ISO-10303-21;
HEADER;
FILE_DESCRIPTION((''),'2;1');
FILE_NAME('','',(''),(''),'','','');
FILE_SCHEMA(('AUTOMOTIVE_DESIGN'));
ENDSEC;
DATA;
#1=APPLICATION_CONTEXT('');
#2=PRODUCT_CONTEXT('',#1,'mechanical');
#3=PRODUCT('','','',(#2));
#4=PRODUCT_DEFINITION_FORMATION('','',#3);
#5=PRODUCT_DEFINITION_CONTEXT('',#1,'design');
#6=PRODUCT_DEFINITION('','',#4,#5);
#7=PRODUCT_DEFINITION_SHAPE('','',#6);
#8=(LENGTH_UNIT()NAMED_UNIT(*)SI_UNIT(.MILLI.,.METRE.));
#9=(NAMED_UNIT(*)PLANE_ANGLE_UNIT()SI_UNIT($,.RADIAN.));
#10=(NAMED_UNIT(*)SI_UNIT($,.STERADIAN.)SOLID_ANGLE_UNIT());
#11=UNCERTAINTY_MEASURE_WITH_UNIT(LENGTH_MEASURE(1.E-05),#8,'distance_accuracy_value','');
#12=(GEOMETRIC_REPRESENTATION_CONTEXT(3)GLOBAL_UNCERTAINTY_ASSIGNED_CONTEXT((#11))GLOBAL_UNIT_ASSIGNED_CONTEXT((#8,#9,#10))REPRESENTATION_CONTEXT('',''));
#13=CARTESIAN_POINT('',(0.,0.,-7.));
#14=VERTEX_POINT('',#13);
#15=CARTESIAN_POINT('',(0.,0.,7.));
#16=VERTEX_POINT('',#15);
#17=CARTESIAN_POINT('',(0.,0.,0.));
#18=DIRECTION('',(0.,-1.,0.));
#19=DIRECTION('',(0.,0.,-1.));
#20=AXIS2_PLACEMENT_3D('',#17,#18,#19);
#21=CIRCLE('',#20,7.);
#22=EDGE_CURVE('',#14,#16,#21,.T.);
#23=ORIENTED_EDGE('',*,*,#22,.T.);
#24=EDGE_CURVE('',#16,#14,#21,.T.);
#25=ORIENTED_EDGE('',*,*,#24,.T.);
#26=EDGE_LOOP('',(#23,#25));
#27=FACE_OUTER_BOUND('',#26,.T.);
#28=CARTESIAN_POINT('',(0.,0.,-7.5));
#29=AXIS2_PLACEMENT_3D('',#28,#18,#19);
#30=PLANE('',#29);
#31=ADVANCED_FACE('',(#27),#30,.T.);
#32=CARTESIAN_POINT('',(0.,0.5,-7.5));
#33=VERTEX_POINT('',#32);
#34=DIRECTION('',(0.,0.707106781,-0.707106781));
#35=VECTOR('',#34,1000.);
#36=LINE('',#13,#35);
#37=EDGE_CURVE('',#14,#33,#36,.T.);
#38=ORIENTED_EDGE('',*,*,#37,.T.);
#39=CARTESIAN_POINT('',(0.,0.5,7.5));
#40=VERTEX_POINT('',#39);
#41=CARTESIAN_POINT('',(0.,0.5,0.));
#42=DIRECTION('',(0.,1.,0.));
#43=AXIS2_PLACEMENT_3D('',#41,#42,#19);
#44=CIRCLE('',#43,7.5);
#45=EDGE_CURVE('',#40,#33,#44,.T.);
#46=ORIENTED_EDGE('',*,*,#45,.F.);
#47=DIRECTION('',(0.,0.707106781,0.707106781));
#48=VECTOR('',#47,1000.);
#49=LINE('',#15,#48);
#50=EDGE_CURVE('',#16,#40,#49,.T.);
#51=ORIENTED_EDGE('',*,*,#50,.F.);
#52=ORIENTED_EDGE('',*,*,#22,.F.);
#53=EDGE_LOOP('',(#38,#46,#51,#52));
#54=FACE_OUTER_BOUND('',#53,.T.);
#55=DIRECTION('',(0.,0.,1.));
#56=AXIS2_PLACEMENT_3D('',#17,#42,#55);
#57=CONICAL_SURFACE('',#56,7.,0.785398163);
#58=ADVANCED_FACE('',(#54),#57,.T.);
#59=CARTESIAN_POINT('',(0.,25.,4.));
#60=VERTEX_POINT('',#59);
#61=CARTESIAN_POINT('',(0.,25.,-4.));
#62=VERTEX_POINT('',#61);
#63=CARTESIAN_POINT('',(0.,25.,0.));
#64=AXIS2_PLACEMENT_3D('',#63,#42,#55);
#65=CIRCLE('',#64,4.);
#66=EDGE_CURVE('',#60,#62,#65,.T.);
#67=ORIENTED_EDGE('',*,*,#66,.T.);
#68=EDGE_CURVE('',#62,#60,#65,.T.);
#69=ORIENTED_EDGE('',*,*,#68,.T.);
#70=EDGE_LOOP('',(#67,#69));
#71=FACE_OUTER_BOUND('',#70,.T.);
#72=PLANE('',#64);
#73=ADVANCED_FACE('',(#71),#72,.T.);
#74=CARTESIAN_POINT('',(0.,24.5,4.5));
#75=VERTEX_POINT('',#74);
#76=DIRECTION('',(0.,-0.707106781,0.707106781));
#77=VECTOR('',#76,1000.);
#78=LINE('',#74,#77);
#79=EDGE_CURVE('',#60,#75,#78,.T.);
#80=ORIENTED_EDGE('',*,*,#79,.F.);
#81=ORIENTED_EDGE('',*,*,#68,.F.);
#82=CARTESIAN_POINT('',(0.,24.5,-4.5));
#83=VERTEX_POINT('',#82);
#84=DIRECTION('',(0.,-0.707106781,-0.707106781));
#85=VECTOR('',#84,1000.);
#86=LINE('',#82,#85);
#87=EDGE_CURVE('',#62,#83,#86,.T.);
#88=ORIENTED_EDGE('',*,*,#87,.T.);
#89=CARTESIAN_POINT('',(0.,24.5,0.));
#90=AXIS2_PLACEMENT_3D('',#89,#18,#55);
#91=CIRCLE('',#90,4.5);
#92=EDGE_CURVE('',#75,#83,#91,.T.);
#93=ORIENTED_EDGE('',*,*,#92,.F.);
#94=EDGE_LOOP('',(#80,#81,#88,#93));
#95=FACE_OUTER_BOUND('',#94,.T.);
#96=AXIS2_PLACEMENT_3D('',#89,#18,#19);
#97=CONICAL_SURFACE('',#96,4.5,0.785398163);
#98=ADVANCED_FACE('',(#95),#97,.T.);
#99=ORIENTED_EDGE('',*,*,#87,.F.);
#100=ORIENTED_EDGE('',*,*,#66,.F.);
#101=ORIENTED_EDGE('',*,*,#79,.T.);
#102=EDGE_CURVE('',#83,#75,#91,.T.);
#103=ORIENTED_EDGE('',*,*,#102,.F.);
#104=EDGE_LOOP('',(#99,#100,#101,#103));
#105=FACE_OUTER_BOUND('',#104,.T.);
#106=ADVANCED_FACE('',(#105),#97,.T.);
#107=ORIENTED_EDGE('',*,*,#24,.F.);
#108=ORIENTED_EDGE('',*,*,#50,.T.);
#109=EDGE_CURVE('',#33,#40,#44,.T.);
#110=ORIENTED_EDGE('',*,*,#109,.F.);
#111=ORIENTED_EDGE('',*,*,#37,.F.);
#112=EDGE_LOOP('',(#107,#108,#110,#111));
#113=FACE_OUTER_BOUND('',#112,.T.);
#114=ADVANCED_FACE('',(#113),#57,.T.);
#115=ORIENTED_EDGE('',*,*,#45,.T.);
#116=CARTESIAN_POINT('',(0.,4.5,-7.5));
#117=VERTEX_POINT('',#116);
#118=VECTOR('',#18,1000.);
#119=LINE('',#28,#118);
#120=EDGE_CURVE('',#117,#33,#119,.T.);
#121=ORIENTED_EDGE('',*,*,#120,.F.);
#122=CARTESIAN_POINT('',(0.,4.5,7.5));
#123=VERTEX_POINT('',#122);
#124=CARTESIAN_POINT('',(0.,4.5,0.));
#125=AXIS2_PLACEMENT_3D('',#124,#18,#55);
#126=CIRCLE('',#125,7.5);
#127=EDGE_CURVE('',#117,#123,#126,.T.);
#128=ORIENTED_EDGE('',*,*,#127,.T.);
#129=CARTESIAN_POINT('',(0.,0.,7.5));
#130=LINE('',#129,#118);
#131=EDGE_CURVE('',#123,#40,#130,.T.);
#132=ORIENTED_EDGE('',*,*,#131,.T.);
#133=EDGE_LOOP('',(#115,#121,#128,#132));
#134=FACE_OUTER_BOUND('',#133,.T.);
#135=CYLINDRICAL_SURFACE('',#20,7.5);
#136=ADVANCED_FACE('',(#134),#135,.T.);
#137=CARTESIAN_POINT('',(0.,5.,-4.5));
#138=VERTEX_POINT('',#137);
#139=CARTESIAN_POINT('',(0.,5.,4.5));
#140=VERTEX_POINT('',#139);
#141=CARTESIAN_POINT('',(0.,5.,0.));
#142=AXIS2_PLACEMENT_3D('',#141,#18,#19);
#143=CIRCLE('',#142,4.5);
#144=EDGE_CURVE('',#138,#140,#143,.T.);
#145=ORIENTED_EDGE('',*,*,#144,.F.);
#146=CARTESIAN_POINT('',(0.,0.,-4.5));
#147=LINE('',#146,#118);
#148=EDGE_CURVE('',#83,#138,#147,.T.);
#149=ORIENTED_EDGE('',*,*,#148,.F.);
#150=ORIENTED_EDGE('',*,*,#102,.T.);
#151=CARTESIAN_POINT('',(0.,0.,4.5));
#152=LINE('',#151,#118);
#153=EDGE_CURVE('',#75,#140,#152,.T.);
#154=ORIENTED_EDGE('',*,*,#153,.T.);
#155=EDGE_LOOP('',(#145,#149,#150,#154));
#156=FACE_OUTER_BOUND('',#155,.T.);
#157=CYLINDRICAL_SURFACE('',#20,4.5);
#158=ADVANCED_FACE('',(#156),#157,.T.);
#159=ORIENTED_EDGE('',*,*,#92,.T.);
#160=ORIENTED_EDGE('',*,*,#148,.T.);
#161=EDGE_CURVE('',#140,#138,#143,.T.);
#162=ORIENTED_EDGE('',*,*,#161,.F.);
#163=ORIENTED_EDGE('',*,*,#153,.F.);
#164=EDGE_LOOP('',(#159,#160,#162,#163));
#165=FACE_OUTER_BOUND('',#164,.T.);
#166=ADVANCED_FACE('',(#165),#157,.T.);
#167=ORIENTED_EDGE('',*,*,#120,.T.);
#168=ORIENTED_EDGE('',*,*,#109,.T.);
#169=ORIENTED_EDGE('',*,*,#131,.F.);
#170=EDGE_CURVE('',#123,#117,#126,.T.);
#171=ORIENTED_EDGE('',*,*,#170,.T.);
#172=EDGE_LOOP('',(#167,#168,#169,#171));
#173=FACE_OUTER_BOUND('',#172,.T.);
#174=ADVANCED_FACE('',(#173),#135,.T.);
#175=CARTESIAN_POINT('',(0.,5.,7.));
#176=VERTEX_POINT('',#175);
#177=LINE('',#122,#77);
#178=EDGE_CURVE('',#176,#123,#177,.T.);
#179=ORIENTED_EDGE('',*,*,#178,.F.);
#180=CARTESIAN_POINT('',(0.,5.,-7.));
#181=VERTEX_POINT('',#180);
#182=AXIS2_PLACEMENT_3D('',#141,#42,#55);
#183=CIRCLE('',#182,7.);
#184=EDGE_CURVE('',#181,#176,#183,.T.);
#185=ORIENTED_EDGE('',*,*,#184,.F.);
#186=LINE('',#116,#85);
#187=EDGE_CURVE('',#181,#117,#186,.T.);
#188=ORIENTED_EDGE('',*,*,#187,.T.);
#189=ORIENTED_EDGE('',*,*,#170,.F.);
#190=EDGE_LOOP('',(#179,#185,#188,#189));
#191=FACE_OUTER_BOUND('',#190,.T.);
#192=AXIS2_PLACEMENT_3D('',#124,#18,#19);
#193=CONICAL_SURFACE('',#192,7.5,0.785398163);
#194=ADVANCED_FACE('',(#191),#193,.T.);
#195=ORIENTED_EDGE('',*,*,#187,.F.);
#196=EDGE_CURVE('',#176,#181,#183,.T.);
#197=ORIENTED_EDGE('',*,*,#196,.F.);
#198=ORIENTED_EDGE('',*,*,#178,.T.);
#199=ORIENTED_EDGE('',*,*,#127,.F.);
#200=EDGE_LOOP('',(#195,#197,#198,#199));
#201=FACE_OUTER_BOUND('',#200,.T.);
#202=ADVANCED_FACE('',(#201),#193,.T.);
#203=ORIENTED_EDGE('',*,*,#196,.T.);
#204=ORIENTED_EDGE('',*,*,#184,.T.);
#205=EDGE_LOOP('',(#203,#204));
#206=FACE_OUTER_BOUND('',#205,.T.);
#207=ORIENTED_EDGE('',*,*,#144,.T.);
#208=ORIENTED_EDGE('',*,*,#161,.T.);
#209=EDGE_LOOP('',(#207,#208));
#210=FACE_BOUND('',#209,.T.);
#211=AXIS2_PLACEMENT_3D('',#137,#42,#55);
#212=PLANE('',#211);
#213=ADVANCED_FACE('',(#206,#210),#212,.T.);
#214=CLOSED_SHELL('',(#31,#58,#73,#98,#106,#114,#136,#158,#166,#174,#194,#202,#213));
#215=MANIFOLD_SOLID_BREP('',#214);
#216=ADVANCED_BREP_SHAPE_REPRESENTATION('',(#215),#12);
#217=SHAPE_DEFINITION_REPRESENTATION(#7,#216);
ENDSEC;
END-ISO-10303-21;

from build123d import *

# Parameters (mm, degrees)
CHAMFER1_SIZE = 0.5


with BuildPart() as part:
    # Sketch1 → Revolve1 (revolve)
    with BuildSketch(Plane(origin=(0, 0, 0), x_dir=(0, 0, -1), z_dir=(1, 0, 0))):
        Polygon((0, 25), (4.5, 25), (4.5, 5), (7.5, 5), (7.5, 0), (0, 0), align=None)
    revolve(axis=Axis((0, 0, 0), (0, 1, 0)))

    # Chamfer1
    chamfer1_edges = [part.edges().sort_by_distance(p)[0] for p in [
        (0, 0, 7.5),
        (0, 5, 7.5),
        (0, 25, 4.5),
    ]]
    chamfer(chamfer1_edges, length=CHAMFER1_SIZE)


solid = part.part
